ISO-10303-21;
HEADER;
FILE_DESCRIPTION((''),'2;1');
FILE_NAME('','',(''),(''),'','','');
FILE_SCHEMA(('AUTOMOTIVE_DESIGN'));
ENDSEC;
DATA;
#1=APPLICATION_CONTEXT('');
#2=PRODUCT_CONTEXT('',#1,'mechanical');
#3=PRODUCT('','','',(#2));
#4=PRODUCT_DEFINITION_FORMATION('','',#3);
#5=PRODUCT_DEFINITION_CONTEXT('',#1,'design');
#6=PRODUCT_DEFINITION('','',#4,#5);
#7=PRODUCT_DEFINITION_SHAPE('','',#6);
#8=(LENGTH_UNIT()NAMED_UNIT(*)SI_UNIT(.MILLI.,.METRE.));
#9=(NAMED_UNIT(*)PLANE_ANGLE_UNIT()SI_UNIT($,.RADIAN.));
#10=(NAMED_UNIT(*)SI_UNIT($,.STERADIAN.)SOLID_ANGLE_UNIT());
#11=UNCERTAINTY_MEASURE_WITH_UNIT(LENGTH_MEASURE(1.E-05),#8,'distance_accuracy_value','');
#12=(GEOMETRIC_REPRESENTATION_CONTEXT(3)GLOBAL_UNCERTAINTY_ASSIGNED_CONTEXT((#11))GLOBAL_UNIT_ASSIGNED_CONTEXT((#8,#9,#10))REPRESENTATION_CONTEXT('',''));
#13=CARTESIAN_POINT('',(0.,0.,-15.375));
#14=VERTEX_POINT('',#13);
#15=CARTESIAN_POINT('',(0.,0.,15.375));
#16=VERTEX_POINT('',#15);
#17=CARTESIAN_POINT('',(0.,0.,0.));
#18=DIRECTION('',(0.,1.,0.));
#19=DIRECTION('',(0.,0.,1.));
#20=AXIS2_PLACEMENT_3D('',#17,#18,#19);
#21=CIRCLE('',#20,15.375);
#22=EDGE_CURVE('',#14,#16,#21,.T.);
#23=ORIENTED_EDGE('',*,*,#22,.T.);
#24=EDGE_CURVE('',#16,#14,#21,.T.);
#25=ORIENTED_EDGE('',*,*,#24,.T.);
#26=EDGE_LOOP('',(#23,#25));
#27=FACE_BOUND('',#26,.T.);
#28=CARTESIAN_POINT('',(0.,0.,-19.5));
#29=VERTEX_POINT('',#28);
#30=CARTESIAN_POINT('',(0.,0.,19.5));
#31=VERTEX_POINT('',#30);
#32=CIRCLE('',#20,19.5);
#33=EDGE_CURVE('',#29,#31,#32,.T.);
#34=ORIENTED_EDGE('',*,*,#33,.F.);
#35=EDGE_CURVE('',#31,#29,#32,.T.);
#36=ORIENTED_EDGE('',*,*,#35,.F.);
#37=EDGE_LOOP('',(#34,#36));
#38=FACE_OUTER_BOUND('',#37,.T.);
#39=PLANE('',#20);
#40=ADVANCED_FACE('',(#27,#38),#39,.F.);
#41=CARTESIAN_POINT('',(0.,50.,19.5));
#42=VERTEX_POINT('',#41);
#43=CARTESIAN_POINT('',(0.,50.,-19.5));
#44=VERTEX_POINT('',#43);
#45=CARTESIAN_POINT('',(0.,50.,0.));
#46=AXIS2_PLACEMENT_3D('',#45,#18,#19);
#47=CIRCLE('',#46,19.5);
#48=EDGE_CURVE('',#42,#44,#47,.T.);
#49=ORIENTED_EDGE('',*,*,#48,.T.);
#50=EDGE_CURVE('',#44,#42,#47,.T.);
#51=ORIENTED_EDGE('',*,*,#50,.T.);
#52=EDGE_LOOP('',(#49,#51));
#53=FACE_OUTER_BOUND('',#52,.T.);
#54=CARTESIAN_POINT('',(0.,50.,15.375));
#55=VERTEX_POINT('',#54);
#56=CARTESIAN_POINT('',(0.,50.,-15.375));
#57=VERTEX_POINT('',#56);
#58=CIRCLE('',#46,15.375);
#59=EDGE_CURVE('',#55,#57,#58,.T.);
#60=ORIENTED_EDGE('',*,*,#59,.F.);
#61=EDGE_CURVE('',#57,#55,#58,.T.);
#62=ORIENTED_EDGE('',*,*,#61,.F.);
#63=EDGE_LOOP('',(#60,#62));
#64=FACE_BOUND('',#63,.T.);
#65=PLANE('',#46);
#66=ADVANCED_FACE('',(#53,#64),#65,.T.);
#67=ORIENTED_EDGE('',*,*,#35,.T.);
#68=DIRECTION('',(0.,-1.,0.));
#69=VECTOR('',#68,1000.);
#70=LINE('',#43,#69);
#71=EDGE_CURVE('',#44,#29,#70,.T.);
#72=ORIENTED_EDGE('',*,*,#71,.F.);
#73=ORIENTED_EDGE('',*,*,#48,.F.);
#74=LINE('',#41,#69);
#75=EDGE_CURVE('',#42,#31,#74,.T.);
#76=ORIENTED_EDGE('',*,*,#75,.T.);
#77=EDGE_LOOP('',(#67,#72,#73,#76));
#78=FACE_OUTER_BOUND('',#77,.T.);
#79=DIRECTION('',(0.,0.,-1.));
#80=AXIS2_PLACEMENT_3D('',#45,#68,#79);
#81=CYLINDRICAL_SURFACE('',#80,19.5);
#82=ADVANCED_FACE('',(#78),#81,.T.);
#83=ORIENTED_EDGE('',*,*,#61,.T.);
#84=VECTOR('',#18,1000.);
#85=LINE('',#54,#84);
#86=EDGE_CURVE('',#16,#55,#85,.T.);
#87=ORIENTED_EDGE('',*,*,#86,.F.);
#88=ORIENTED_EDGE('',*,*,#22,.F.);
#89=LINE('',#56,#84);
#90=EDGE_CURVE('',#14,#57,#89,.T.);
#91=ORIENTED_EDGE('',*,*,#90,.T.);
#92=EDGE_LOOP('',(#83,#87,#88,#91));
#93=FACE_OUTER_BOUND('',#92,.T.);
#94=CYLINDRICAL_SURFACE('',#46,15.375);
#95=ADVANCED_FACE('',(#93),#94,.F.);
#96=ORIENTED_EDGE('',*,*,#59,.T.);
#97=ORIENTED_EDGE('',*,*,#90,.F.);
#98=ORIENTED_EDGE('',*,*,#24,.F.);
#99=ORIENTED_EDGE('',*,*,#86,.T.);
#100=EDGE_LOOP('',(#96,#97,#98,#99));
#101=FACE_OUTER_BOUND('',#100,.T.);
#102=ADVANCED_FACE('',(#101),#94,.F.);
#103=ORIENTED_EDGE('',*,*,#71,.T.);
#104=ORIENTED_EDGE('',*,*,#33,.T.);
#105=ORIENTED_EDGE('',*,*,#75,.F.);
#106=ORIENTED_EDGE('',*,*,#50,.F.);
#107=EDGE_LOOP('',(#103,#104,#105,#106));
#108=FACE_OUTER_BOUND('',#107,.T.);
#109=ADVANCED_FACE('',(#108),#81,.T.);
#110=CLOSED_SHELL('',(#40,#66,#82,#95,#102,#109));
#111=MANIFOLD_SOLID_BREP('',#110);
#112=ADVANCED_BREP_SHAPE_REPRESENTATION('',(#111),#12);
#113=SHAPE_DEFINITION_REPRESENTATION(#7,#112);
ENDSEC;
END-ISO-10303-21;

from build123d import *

# Parameters (mm, degrees)
SKETCH1_R           = 19.5
BOSS_EXTRUDE1_DEPTH = 50
G1_TAPPED_HOLE1_D   = 30.75


with BuildPart() as part:
    # Sketch1 → Boss-Extrude1 (new body)
    with BuildSketch(Plane(origin=(0, 0, 0), x_dir=(1, 0, 0), z_dir=(0, 1, 0))):
        with Locations(Location((0, 0, 0), (0, 0, 270))):
            Circle(SKETCH1_R)
    extrude(amount=BOSS_EXTRUDE1_DEPTH)

    # G1 Tapped Hole1 (through all)
    with Locations(Plane.ZX.offset(50)):
        with Locations((0, 0)):
            Hole(G1_TAPPED_HOLE1_D / 2)


solid = part.part
